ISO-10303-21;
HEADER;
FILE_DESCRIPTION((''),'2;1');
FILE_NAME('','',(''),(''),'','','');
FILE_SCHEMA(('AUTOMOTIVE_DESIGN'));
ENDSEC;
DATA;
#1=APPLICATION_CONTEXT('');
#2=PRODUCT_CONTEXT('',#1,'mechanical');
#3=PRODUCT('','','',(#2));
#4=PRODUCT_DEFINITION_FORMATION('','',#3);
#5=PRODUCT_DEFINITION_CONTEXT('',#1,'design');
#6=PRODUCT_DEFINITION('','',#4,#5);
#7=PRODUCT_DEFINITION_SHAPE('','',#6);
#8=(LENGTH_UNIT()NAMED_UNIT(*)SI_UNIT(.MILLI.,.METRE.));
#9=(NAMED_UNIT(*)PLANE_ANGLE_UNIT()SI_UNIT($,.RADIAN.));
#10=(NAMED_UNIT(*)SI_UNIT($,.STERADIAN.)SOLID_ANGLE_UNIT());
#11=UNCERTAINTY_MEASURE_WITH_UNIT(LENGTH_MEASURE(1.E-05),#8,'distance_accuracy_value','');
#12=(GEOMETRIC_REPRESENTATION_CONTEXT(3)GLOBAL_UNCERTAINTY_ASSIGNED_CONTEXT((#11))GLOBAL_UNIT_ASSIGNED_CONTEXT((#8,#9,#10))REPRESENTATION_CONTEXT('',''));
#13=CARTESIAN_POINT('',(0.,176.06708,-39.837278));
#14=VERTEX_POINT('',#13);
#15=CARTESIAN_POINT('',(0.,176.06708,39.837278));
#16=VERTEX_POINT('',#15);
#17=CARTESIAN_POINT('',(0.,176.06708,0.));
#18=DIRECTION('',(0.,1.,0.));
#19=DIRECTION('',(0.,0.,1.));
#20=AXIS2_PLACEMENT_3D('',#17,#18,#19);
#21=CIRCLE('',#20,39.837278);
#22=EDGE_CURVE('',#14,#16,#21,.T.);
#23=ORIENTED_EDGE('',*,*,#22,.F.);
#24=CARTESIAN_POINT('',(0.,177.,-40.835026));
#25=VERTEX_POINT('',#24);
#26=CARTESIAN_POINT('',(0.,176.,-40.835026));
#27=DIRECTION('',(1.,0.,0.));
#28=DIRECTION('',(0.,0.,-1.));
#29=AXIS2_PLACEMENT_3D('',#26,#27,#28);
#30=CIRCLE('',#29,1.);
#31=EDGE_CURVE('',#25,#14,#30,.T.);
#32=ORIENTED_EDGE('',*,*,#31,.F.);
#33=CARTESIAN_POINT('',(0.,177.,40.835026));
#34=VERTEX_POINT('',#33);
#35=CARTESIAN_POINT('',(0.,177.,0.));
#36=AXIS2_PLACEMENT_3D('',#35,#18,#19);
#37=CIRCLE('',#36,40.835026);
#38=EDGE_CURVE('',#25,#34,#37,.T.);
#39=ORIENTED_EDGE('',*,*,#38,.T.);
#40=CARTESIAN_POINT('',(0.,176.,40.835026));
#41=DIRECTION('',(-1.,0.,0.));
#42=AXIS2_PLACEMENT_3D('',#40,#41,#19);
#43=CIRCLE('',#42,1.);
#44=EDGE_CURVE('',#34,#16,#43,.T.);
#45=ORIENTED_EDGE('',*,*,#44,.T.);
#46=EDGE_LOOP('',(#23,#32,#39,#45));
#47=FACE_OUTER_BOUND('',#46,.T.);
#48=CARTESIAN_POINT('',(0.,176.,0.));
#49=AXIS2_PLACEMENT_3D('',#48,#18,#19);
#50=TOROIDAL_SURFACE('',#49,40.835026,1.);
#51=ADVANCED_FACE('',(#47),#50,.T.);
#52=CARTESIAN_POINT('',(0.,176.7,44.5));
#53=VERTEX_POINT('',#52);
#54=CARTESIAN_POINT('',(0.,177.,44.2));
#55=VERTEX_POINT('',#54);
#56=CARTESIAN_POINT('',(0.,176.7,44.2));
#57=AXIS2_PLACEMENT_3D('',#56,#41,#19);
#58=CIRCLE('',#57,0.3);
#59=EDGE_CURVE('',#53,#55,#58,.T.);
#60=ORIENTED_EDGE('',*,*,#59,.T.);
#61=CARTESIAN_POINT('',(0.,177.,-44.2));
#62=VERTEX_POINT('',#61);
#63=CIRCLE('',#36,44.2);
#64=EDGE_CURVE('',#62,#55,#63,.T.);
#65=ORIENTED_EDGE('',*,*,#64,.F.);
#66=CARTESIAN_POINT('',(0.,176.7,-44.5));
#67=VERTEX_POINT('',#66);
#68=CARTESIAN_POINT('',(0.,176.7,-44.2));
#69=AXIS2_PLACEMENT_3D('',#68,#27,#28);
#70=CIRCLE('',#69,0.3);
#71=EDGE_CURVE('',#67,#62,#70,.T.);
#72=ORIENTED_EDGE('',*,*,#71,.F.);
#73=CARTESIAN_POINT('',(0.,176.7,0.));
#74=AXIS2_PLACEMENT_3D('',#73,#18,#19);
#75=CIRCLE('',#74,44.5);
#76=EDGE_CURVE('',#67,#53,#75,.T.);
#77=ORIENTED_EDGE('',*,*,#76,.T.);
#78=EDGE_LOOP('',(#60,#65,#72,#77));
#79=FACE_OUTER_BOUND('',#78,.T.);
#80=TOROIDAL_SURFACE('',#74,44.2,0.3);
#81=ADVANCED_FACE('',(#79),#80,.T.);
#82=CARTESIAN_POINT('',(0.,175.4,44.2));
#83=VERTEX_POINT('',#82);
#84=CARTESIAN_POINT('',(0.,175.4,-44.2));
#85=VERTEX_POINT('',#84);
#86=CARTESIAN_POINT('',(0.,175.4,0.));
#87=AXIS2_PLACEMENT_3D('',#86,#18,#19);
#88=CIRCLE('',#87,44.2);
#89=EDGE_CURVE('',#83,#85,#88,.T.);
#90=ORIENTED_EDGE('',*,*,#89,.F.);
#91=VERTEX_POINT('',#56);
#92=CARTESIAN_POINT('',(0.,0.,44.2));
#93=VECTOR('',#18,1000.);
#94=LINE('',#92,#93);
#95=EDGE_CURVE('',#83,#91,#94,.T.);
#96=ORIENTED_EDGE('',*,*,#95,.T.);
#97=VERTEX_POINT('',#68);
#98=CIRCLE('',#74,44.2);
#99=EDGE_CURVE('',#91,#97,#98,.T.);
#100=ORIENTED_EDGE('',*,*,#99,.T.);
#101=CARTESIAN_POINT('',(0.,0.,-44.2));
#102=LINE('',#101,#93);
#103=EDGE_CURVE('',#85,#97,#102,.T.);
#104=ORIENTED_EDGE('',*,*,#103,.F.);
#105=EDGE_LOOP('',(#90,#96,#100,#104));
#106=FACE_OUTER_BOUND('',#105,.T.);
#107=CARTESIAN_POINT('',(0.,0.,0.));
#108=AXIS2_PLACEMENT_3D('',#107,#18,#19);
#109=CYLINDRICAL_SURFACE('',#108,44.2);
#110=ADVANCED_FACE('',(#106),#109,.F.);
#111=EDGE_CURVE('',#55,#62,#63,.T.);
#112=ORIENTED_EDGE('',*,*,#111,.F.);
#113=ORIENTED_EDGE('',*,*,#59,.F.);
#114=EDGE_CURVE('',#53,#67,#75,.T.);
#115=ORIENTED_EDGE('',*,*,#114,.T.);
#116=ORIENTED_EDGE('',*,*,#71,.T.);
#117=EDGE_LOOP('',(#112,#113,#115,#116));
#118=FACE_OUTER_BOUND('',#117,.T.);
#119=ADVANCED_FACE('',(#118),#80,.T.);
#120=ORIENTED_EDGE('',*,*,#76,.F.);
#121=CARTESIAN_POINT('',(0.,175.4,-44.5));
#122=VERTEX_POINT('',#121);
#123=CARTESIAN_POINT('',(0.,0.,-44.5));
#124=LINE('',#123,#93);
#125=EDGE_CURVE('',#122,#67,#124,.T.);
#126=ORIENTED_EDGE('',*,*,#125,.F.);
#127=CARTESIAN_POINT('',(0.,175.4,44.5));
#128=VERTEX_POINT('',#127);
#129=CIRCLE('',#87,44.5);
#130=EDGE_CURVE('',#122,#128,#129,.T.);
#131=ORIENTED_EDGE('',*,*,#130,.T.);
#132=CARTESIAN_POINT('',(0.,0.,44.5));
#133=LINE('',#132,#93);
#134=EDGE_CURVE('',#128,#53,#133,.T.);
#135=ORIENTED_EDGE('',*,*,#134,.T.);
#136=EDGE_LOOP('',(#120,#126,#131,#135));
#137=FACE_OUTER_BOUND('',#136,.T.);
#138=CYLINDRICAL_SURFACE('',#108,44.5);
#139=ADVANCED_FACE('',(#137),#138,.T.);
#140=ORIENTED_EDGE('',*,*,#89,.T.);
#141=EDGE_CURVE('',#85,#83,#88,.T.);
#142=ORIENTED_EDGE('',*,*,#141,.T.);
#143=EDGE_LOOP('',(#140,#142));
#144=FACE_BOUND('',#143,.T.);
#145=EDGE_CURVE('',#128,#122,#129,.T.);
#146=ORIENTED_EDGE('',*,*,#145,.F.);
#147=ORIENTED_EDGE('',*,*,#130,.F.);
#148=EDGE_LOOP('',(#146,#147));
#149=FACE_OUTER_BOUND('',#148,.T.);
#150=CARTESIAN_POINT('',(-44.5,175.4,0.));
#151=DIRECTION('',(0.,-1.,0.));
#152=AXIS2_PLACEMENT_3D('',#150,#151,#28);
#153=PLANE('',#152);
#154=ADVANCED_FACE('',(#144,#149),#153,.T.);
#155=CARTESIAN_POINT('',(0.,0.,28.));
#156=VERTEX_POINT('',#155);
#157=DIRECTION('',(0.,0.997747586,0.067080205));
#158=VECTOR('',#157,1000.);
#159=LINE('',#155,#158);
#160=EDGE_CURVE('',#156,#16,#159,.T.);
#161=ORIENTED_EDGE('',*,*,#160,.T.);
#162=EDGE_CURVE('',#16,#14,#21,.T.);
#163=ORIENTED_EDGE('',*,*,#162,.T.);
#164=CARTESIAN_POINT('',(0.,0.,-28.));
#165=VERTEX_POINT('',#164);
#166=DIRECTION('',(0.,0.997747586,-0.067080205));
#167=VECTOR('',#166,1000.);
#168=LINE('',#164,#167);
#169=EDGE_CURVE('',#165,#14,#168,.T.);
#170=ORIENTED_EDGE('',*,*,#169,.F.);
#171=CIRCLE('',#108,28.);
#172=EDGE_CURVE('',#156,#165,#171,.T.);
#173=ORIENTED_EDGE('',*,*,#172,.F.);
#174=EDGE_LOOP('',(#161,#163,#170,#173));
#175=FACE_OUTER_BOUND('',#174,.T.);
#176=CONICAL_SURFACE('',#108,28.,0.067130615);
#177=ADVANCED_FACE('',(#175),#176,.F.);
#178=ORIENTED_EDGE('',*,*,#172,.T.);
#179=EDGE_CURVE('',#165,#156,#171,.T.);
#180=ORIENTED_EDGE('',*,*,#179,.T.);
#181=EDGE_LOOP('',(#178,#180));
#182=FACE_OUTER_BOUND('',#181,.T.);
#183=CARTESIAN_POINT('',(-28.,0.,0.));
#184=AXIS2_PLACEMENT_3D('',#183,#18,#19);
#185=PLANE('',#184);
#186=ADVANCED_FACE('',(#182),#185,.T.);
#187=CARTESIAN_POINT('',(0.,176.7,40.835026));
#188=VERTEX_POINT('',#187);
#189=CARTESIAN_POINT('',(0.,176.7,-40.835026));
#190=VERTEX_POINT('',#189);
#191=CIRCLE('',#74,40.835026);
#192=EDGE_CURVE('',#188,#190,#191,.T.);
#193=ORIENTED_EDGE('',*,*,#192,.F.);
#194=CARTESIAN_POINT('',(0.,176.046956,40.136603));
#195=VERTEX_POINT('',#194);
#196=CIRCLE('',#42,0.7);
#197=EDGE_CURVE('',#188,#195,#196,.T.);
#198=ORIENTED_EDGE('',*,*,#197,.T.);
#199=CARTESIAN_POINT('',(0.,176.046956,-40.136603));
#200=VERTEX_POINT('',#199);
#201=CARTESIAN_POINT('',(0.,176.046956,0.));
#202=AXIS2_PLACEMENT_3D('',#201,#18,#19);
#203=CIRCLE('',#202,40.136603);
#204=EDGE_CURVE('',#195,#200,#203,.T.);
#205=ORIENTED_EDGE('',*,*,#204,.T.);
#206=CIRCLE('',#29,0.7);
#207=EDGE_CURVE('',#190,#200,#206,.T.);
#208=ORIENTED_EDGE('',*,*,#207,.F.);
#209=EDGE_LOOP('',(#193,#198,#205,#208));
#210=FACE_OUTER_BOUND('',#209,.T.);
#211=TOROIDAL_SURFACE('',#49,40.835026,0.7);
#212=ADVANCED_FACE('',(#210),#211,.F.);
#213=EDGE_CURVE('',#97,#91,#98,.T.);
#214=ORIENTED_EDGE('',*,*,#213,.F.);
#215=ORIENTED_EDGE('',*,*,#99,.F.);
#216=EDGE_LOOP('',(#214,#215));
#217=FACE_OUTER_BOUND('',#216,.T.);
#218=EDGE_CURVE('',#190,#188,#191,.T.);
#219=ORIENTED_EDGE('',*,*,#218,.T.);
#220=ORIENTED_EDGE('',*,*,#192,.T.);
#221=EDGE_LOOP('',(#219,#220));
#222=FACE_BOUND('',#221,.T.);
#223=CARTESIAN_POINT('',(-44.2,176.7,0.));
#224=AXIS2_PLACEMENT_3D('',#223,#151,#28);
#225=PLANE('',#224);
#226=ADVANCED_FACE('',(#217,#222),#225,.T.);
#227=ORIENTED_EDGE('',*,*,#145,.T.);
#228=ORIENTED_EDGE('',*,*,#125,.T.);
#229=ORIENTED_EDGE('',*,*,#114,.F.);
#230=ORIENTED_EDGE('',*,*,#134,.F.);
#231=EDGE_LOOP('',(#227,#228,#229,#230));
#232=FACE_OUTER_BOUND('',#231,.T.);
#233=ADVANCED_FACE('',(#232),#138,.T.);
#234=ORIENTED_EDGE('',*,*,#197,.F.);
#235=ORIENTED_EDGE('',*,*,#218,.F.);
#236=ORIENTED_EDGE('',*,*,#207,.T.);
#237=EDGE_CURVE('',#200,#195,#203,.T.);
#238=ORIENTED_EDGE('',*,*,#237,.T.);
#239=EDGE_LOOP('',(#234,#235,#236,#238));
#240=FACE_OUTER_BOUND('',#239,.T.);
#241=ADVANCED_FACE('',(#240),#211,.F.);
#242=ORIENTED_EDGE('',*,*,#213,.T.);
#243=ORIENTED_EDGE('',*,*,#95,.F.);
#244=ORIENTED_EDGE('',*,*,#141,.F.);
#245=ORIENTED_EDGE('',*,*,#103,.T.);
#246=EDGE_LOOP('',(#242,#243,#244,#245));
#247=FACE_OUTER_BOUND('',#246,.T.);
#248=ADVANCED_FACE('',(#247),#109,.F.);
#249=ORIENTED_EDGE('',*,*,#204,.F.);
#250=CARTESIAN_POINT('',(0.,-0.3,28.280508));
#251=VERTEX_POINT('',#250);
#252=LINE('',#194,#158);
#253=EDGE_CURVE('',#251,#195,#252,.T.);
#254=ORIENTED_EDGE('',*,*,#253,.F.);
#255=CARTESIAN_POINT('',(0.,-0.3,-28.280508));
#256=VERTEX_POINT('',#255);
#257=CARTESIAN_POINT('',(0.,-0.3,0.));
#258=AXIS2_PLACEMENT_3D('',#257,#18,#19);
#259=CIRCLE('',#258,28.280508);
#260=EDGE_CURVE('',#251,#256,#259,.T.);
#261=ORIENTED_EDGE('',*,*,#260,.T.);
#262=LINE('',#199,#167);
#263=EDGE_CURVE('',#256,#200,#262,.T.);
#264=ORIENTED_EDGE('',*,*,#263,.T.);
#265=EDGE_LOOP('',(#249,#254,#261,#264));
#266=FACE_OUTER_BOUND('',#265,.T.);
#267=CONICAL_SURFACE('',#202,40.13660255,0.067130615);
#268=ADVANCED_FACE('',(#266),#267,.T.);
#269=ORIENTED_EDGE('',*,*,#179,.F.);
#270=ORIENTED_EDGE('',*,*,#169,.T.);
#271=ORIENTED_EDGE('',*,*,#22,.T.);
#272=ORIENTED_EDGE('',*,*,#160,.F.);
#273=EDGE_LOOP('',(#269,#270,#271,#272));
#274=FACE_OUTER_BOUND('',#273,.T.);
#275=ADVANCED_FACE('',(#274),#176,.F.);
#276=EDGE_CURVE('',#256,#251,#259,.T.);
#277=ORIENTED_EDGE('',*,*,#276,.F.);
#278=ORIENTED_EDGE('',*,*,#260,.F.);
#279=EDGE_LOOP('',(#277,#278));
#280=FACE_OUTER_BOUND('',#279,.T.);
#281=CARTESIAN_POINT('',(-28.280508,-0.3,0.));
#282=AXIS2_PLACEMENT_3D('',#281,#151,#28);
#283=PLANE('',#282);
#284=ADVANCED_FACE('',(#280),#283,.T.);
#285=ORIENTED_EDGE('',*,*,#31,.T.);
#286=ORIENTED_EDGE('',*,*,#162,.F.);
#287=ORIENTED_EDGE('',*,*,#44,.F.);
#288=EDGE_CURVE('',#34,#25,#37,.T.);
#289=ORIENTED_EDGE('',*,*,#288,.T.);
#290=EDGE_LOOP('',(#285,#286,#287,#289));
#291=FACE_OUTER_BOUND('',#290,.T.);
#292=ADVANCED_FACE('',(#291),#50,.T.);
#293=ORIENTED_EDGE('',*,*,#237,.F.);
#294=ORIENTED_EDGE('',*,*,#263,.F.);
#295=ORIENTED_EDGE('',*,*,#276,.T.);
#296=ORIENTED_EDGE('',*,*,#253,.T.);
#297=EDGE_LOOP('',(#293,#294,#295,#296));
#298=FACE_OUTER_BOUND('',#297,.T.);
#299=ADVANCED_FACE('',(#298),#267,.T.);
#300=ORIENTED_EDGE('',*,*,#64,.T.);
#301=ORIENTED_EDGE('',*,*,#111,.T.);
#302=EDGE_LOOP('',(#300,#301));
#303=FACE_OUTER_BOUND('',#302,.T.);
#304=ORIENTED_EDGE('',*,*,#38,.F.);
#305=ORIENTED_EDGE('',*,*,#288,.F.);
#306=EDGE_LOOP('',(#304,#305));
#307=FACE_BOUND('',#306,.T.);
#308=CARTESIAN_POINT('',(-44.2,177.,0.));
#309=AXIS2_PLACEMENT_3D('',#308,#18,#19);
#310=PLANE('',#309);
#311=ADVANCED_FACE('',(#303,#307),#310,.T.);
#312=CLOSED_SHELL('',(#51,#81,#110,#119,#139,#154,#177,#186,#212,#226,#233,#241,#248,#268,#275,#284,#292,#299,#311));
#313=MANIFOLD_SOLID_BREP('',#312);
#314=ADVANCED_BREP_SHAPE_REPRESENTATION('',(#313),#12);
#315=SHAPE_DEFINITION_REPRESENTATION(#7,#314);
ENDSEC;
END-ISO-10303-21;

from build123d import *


with BuildPart() as part:
    # 草图1 → 旋转1 (revolve)
    with BuildSketch(Plane.XY, mode=Mode.PRIVATE) as revolve_1_sk:
        with BuildLine():
            Line((-44.2, 177), (-40.83502586, 177))
            ThreePointArc((-40.83502586, 177), (-40.152047165, 176.730438295), (-39.837278274, 176.067080205))
            Line((-39.837278274, 176.067080205), (-28, 0))
            Line((-28, 0), (0, 0))
            Line((0, 0), (0, -0.3))
            Line((0, -0.3), (-28.280507758, -0.3))
            Line((-28.280507758, -0.3), (-40.13660255, 176.046956143))
            ThreePointArc((-40.13660255, 176.046956143), (-40.356940774, 176.511306806), (-40.83502586, 176.7))
            Line((-40.83502586, 176.7), (-44.2, 176.7))
            Line((-44.2, 176.7), (-44.2, 175.4))
            Line((-44.2, 175.4), (-44.5, 175.4))
            Line((-44.5, 175.4), (-44.5, 176.7))
            ThreePointArc((-44.5, 176.7), (-44.412132034, 176.912132034), (-44.2, 177))
        make_face()
    revolve(revolve_1_sk.sketch.rotate(Axis((0, 0, 0), (0, -1, 0)), 270), axis=Axis((0, 0, 0), (0, -1, 0)))


solid = part.part
